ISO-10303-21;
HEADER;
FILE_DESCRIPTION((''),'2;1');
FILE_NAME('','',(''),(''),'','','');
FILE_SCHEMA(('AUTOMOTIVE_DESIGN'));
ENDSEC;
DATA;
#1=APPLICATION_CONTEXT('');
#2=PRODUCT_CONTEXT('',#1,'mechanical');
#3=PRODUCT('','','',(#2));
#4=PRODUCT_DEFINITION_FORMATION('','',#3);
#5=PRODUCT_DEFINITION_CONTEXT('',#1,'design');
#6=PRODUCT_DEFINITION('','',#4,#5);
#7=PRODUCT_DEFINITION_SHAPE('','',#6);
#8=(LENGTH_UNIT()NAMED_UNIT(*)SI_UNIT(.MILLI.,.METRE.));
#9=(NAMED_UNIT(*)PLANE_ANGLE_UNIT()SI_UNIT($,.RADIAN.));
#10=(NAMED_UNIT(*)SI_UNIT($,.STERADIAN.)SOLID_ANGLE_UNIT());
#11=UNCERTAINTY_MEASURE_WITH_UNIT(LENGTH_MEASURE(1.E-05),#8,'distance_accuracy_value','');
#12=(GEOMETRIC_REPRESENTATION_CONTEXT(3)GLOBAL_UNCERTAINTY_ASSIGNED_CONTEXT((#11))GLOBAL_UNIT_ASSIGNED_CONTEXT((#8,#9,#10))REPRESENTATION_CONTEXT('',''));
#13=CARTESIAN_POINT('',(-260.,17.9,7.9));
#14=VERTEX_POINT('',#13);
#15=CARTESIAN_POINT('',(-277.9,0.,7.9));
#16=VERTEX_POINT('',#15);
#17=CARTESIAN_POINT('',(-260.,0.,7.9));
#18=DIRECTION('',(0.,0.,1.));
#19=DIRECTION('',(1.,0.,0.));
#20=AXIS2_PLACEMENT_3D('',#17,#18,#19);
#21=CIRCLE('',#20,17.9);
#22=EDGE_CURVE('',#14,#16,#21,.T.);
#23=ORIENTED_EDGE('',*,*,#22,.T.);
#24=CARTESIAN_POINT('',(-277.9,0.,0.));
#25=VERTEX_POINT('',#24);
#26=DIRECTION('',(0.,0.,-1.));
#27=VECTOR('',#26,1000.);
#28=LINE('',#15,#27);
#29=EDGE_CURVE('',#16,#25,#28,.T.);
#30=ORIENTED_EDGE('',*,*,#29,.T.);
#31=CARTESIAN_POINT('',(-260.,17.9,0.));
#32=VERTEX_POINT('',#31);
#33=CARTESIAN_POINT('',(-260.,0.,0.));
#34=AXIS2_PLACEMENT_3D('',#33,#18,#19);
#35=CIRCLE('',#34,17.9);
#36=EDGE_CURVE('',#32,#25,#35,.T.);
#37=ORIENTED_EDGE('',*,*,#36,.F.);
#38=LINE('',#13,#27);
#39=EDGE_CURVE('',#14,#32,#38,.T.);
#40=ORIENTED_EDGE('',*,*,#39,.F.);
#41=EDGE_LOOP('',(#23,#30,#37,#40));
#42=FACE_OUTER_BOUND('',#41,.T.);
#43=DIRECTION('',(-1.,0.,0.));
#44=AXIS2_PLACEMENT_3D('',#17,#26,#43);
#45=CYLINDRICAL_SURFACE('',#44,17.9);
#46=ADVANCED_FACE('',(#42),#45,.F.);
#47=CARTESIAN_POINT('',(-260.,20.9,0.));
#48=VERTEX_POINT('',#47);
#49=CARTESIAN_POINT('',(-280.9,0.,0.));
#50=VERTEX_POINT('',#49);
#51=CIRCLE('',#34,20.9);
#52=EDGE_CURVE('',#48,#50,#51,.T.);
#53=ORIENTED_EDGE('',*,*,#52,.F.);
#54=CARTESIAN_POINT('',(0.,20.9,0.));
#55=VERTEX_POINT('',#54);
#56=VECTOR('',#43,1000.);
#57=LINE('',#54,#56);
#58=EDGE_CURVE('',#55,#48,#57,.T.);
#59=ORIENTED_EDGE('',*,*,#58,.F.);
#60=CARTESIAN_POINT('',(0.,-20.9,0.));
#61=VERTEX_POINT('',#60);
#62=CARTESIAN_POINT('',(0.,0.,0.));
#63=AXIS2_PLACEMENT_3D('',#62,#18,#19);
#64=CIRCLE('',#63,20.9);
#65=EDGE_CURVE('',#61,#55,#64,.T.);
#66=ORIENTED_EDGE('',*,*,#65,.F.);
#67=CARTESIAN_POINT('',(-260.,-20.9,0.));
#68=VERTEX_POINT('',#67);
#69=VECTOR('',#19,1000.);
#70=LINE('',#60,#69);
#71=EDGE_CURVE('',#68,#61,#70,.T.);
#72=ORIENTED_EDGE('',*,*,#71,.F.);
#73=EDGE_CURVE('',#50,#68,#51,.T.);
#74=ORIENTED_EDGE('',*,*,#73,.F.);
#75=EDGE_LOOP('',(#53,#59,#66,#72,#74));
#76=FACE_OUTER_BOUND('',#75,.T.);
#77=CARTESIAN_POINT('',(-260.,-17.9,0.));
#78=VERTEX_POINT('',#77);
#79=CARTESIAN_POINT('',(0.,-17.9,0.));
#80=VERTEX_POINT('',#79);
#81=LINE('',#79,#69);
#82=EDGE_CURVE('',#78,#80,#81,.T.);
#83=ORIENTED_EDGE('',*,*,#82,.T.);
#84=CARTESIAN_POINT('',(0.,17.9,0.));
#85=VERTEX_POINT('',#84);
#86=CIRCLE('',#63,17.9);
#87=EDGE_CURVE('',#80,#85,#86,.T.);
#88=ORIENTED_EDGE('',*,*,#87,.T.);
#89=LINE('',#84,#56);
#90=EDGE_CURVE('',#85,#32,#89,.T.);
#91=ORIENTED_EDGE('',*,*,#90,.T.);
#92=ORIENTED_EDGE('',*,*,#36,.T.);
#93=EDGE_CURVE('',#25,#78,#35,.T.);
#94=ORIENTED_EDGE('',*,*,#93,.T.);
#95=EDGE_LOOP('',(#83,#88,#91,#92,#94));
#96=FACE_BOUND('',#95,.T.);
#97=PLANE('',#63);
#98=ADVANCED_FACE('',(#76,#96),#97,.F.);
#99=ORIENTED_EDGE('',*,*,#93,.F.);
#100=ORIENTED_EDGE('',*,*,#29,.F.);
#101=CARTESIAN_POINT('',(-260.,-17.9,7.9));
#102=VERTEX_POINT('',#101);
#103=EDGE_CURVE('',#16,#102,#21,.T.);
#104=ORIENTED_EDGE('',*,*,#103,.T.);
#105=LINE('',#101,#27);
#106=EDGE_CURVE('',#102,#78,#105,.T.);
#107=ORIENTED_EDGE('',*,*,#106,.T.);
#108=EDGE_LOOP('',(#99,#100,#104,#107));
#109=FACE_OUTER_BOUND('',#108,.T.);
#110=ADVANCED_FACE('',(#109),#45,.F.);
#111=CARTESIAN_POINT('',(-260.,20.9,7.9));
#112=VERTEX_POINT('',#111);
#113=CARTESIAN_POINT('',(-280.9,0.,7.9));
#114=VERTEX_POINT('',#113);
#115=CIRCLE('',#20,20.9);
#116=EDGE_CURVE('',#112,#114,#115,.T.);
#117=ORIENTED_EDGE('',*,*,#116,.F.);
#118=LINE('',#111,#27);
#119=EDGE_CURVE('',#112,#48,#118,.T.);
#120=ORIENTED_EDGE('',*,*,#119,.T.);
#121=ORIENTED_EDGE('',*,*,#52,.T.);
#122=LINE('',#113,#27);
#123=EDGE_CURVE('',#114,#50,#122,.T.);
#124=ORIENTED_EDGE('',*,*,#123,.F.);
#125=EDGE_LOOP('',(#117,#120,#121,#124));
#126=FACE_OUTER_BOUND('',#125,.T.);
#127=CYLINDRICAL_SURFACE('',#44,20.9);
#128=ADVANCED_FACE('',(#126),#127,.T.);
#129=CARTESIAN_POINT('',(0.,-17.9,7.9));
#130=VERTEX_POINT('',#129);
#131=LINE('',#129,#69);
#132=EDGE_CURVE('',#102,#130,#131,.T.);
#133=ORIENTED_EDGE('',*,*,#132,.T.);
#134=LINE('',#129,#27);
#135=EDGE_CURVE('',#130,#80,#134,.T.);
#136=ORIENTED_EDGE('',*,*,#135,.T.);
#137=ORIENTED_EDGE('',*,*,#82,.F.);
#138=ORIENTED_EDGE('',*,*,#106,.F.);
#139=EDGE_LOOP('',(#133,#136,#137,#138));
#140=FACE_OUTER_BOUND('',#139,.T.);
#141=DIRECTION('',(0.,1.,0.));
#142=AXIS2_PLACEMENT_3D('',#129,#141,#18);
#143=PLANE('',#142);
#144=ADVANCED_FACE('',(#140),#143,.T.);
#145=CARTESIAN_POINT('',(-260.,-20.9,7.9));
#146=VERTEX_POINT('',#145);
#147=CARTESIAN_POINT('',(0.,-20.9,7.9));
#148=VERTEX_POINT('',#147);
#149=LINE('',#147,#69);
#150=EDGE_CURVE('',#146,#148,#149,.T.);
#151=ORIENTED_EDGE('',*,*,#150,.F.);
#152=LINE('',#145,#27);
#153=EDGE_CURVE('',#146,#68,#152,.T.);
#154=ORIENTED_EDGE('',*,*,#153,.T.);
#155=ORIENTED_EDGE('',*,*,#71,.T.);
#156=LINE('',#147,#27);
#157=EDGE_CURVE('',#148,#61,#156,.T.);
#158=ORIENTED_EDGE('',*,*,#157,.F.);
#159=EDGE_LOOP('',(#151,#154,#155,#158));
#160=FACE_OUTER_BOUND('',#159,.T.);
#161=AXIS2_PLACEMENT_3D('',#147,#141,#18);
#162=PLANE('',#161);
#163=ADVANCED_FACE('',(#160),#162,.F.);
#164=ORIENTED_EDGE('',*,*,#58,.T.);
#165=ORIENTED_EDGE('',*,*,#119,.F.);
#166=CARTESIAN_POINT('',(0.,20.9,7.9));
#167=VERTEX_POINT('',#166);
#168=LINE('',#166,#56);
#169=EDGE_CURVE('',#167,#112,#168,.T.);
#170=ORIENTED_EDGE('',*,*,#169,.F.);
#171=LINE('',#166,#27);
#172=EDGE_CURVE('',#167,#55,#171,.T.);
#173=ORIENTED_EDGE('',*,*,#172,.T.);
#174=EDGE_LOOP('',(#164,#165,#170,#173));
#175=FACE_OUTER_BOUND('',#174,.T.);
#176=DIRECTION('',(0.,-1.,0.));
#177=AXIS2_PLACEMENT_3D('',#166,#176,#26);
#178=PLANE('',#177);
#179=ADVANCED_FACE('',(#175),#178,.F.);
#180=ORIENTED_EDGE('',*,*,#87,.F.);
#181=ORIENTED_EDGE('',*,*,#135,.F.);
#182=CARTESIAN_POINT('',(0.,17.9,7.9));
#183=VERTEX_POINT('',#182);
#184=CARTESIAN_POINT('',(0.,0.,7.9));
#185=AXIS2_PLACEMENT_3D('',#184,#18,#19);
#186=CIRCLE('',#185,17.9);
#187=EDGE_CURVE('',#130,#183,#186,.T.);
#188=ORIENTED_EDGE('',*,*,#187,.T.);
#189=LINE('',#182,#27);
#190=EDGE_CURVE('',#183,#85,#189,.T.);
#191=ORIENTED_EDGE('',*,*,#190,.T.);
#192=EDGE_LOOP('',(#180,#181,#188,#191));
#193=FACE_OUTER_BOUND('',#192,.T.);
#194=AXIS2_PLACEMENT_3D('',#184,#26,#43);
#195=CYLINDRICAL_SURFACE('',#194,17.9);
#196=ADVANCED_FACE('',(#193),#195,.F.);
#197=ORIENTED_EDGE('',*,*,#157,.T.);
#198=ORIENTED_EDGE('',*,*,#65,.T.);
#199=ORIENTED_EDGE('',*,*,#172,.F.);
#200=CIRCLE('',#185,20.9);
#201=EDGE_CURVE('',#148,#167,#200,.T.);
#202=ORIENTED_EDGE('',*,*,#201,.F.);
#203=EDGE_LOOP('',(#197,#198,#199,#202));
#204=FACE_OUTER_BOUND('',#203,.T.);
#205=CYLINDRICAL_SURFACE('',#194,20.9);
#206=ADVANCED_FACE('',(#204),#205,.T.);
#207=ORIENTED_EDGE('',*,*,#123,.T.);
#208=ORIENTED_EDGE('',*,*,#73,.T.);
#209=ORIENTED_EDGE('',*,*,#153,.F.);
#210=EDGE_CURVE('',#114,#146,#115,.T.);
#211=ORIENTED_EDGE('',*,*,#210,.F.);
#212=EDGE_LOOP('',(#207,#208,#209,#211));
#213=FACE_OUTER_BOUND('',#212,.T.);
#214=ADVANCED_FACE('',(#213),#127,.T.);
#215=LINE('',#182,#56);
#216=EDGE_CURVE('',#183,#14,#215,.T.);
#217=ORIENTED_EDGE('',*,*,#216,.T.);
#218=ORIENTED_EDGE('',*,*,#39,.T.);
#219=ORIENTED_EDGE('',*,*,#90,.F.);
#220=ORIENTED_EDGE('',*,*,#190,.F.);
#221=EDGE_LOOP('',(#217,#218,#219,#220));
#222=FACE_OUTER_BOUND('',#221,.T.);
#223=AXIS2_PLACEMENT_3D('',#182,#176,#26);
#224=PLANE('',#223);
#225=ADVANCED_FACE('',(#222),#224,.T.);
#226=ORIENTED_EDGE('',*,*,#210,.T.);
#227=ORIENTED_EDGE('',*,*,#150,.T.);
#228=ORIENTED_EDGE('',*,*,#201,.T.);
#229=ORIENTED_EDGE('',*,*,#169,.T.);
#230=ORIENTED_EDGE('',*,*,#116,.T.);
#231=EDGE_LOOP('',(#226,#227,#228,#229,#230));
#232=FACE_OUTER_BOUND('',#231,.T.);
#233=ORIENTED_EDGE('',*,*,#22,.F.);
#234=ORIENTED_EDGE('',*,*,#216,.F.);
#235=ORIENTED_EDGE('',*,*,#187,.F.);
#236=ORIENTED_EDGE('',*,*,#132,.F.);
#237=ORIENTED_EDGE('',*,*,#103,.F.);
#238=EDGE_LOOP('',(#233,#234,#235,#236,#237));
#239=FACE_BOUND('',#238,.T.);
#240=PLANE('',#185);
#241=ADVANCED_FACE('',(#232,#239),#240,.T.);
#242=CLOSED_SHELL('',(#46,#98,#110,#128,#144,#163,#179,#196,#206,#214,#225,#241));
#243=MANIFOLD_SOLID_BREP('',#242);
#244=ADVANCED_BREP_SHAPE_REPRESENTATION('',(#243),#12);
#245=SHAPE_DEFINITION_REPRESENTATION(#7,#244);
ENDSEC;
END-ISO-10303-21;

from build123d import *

# Parameters (mm, degrees)
BOSS_EXTRUDE1_DEPTH = 7.9
SHELL1_T            = -3


with BuildPart() as part:
    # Sketch2 → Boss-Extrude1 (new body)
    with BuildSketch(Plane.XY):
        with BuildLine():
            Line((0, 20.9), (-260, 20.9))
            ThreePointArc((-260, 20.9), (-280.9, 0), (-260, -20.9))
            Line((-260, -20.9), (0, -20.9))
            ThreePointArc((0, -20.9), (20.9, 0), (0, 20.9))
        make_face()
    extrude(amount=BOSS_EXTRUDE1_DEPTH)

    # Shell1
    shell1_openings = [part.faces().sort_by_distance(p)[0] for p in [
        (-130, 0, 7.9),
        (-130, 0, 0),
    ]]
    offset(amount=SHELL1_T, openings=shell1_openings, kind=Kind.INTERSECTION)


solid = part.part
